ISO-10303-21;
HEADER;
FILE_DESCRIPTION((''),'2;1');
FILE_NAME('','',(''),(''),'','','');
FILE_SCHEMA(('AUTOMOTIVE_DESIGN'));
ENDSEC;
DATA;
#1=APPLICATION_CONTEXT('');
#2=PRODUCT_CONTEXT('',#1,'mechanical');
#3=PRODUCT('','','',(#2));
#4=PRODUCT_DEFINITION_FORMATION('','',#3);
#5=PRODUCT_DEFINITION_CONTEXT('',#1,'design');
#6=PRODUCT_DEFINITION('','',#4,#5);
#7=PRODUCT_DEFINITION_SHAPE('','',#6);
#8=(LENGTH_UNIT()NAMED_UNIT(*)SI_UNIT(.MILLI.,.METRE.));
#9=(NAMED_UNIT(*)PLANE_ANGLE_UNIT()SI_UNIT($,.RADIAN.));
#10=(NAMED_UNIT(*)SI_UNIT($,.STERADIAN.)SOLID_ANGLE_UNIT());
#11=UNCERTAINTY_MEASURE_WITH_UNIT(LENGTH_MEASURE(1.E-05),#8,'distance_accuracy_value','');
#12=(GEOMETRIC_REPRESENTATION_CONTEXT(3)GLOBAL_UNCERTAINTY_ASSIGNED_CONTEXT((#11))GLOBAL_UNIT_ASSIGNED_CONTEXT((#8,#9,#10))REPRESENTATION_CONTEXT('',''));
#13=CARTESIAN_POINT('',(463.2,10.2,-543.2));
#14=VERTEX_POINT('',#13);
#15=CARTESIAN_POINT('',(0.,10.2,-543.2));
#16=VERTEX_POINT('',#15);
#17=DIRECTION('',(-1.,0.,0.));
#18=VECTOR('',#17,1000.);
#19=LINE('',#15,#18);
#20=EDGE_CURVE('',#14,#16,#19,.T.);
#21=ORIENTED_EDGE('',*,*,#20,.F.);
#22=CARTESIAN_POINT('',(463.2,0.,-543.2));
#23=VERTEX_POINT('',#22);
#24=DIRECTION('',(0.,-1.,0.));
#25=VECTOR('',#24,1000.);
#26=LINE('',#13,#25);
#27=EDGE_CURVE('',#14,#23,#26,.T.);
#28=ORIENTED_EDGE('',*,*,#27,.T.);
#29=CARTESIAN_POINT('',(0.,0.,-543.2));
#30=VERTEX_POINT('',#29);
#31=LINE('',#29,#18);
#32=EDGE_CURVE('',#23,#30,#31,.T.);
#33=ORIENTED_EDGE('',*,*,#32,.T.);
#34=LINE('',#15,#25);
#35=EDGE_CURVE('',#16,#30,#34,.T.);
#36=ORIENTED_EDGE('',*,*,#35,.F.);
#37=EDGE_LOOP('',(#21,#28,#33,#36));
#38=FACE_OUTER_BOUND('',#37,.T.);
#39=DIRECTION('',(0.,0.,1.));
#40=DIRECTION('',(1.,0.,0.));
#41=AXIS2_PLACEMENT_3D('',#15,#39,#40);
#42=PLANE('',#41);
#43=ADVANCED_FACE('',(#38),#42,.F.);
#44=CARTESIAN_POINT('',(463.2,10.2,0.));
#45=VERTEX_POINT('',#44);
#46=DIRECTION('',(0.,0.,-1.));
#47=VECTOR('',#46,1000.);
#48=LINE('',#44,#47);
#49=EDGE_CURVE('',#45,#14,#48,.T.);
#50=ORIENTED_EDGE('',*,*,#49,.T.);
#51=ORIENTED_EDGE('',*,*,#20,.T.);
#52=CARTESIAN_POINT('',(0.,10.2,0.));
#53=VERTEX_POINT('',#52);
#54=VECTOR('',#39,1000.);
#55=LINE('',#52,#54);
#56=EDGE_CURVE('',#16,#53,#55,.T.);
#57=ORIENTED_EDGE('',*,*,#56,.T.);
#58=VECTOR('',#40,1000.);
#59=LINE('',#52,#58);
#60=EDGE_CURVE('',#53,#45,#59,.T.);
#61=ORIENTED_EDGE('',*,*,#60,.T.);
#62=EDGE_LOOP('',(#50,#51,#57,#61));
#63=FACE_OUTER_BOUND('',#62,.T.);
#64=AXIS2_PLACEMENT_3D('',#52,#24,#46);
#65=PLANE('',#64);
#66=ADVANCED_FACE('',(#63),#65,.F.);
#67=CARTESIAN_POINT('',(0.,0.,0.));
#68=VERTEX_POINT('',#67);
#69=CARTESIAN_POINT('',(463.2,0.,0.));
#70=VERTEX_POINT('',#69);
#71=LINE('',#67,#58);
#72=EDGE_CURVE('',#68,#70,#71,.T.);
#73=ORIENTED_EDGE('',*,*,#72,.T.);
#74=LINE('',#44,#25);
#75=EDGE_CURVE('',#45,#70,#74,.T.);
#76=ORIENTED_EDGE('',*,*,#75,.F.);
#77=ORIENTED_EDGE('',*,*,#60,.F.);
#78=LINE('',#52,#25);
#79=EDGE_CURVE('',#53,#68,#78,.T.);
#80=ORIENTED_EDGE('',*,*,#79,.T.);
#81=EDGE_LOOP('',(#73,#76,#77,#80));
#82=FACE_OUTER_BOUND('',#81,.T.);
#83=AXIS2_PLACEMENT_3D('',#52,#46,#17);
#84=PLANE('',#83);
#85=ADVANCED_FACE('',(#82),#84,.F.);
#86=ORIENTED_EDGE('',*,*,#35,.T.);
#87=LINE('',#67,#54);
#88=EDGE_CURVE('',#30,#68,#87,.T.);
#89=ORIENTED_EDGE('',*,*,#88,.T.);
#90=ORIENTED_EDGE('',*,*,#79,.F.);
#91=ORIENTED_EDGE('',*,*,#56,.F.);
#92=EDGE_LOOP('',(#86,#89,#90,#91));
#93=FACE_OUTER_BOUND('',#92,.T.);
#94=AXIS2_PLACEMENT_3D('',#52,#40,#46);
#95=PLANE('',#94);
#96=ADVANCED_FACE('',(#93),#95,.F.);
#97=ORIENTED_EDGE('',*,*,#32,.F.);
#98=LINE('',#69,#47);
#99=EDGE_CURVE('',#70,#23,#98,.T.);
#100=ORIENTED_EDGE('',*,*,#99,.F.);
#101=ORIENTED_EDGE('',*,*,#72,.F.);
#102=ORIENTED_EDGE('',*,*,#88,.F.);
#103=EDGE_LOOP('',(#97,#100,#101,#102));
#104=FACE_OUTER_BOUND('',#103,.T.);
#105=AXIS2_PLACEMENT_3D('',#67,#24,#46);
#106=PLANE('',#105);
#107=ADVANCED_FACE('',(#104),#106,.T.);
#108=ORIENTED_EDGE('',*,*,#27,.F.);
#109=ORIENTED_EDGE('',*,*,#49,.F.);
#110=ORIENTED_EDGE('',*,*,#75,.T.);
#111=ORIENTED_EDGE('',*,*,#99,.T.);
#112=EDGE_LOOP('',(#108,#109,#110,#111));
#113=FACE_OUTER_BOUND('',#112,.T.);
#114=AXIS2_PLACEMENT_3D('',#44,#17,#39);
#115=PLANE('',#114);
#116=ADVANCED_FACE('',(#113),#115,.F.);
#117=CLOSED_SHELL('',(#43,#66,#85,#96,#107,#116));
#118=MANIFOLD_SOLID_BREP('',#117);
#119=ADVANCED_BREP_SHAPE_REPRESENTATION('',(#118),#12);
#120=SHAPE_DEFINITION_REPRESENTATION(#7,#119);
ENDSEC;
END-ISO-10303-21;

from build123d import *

# Parameters (mm, degrees)
SKETCH1_W           = 463.2
SKETCH1_H           = 543.2
BOSS_EXTRUDE1_DEPTH = 10.2


with BuildPart() as part:
    # Sketch1 → Boss-Extrude1 (new body)
    with BuildSketch(Plane(origin=(0, 0, 0), x_dir=(1, 0, 0), z_dir=(0, 1, 0))):
        with Locations((231.6, 271.6)):
            Rectangle(SKETCH1_W, SKETCH1_H)
    extrude(amount=BOSS_EXTRUDE1_DEPTH)


solid = part.part
